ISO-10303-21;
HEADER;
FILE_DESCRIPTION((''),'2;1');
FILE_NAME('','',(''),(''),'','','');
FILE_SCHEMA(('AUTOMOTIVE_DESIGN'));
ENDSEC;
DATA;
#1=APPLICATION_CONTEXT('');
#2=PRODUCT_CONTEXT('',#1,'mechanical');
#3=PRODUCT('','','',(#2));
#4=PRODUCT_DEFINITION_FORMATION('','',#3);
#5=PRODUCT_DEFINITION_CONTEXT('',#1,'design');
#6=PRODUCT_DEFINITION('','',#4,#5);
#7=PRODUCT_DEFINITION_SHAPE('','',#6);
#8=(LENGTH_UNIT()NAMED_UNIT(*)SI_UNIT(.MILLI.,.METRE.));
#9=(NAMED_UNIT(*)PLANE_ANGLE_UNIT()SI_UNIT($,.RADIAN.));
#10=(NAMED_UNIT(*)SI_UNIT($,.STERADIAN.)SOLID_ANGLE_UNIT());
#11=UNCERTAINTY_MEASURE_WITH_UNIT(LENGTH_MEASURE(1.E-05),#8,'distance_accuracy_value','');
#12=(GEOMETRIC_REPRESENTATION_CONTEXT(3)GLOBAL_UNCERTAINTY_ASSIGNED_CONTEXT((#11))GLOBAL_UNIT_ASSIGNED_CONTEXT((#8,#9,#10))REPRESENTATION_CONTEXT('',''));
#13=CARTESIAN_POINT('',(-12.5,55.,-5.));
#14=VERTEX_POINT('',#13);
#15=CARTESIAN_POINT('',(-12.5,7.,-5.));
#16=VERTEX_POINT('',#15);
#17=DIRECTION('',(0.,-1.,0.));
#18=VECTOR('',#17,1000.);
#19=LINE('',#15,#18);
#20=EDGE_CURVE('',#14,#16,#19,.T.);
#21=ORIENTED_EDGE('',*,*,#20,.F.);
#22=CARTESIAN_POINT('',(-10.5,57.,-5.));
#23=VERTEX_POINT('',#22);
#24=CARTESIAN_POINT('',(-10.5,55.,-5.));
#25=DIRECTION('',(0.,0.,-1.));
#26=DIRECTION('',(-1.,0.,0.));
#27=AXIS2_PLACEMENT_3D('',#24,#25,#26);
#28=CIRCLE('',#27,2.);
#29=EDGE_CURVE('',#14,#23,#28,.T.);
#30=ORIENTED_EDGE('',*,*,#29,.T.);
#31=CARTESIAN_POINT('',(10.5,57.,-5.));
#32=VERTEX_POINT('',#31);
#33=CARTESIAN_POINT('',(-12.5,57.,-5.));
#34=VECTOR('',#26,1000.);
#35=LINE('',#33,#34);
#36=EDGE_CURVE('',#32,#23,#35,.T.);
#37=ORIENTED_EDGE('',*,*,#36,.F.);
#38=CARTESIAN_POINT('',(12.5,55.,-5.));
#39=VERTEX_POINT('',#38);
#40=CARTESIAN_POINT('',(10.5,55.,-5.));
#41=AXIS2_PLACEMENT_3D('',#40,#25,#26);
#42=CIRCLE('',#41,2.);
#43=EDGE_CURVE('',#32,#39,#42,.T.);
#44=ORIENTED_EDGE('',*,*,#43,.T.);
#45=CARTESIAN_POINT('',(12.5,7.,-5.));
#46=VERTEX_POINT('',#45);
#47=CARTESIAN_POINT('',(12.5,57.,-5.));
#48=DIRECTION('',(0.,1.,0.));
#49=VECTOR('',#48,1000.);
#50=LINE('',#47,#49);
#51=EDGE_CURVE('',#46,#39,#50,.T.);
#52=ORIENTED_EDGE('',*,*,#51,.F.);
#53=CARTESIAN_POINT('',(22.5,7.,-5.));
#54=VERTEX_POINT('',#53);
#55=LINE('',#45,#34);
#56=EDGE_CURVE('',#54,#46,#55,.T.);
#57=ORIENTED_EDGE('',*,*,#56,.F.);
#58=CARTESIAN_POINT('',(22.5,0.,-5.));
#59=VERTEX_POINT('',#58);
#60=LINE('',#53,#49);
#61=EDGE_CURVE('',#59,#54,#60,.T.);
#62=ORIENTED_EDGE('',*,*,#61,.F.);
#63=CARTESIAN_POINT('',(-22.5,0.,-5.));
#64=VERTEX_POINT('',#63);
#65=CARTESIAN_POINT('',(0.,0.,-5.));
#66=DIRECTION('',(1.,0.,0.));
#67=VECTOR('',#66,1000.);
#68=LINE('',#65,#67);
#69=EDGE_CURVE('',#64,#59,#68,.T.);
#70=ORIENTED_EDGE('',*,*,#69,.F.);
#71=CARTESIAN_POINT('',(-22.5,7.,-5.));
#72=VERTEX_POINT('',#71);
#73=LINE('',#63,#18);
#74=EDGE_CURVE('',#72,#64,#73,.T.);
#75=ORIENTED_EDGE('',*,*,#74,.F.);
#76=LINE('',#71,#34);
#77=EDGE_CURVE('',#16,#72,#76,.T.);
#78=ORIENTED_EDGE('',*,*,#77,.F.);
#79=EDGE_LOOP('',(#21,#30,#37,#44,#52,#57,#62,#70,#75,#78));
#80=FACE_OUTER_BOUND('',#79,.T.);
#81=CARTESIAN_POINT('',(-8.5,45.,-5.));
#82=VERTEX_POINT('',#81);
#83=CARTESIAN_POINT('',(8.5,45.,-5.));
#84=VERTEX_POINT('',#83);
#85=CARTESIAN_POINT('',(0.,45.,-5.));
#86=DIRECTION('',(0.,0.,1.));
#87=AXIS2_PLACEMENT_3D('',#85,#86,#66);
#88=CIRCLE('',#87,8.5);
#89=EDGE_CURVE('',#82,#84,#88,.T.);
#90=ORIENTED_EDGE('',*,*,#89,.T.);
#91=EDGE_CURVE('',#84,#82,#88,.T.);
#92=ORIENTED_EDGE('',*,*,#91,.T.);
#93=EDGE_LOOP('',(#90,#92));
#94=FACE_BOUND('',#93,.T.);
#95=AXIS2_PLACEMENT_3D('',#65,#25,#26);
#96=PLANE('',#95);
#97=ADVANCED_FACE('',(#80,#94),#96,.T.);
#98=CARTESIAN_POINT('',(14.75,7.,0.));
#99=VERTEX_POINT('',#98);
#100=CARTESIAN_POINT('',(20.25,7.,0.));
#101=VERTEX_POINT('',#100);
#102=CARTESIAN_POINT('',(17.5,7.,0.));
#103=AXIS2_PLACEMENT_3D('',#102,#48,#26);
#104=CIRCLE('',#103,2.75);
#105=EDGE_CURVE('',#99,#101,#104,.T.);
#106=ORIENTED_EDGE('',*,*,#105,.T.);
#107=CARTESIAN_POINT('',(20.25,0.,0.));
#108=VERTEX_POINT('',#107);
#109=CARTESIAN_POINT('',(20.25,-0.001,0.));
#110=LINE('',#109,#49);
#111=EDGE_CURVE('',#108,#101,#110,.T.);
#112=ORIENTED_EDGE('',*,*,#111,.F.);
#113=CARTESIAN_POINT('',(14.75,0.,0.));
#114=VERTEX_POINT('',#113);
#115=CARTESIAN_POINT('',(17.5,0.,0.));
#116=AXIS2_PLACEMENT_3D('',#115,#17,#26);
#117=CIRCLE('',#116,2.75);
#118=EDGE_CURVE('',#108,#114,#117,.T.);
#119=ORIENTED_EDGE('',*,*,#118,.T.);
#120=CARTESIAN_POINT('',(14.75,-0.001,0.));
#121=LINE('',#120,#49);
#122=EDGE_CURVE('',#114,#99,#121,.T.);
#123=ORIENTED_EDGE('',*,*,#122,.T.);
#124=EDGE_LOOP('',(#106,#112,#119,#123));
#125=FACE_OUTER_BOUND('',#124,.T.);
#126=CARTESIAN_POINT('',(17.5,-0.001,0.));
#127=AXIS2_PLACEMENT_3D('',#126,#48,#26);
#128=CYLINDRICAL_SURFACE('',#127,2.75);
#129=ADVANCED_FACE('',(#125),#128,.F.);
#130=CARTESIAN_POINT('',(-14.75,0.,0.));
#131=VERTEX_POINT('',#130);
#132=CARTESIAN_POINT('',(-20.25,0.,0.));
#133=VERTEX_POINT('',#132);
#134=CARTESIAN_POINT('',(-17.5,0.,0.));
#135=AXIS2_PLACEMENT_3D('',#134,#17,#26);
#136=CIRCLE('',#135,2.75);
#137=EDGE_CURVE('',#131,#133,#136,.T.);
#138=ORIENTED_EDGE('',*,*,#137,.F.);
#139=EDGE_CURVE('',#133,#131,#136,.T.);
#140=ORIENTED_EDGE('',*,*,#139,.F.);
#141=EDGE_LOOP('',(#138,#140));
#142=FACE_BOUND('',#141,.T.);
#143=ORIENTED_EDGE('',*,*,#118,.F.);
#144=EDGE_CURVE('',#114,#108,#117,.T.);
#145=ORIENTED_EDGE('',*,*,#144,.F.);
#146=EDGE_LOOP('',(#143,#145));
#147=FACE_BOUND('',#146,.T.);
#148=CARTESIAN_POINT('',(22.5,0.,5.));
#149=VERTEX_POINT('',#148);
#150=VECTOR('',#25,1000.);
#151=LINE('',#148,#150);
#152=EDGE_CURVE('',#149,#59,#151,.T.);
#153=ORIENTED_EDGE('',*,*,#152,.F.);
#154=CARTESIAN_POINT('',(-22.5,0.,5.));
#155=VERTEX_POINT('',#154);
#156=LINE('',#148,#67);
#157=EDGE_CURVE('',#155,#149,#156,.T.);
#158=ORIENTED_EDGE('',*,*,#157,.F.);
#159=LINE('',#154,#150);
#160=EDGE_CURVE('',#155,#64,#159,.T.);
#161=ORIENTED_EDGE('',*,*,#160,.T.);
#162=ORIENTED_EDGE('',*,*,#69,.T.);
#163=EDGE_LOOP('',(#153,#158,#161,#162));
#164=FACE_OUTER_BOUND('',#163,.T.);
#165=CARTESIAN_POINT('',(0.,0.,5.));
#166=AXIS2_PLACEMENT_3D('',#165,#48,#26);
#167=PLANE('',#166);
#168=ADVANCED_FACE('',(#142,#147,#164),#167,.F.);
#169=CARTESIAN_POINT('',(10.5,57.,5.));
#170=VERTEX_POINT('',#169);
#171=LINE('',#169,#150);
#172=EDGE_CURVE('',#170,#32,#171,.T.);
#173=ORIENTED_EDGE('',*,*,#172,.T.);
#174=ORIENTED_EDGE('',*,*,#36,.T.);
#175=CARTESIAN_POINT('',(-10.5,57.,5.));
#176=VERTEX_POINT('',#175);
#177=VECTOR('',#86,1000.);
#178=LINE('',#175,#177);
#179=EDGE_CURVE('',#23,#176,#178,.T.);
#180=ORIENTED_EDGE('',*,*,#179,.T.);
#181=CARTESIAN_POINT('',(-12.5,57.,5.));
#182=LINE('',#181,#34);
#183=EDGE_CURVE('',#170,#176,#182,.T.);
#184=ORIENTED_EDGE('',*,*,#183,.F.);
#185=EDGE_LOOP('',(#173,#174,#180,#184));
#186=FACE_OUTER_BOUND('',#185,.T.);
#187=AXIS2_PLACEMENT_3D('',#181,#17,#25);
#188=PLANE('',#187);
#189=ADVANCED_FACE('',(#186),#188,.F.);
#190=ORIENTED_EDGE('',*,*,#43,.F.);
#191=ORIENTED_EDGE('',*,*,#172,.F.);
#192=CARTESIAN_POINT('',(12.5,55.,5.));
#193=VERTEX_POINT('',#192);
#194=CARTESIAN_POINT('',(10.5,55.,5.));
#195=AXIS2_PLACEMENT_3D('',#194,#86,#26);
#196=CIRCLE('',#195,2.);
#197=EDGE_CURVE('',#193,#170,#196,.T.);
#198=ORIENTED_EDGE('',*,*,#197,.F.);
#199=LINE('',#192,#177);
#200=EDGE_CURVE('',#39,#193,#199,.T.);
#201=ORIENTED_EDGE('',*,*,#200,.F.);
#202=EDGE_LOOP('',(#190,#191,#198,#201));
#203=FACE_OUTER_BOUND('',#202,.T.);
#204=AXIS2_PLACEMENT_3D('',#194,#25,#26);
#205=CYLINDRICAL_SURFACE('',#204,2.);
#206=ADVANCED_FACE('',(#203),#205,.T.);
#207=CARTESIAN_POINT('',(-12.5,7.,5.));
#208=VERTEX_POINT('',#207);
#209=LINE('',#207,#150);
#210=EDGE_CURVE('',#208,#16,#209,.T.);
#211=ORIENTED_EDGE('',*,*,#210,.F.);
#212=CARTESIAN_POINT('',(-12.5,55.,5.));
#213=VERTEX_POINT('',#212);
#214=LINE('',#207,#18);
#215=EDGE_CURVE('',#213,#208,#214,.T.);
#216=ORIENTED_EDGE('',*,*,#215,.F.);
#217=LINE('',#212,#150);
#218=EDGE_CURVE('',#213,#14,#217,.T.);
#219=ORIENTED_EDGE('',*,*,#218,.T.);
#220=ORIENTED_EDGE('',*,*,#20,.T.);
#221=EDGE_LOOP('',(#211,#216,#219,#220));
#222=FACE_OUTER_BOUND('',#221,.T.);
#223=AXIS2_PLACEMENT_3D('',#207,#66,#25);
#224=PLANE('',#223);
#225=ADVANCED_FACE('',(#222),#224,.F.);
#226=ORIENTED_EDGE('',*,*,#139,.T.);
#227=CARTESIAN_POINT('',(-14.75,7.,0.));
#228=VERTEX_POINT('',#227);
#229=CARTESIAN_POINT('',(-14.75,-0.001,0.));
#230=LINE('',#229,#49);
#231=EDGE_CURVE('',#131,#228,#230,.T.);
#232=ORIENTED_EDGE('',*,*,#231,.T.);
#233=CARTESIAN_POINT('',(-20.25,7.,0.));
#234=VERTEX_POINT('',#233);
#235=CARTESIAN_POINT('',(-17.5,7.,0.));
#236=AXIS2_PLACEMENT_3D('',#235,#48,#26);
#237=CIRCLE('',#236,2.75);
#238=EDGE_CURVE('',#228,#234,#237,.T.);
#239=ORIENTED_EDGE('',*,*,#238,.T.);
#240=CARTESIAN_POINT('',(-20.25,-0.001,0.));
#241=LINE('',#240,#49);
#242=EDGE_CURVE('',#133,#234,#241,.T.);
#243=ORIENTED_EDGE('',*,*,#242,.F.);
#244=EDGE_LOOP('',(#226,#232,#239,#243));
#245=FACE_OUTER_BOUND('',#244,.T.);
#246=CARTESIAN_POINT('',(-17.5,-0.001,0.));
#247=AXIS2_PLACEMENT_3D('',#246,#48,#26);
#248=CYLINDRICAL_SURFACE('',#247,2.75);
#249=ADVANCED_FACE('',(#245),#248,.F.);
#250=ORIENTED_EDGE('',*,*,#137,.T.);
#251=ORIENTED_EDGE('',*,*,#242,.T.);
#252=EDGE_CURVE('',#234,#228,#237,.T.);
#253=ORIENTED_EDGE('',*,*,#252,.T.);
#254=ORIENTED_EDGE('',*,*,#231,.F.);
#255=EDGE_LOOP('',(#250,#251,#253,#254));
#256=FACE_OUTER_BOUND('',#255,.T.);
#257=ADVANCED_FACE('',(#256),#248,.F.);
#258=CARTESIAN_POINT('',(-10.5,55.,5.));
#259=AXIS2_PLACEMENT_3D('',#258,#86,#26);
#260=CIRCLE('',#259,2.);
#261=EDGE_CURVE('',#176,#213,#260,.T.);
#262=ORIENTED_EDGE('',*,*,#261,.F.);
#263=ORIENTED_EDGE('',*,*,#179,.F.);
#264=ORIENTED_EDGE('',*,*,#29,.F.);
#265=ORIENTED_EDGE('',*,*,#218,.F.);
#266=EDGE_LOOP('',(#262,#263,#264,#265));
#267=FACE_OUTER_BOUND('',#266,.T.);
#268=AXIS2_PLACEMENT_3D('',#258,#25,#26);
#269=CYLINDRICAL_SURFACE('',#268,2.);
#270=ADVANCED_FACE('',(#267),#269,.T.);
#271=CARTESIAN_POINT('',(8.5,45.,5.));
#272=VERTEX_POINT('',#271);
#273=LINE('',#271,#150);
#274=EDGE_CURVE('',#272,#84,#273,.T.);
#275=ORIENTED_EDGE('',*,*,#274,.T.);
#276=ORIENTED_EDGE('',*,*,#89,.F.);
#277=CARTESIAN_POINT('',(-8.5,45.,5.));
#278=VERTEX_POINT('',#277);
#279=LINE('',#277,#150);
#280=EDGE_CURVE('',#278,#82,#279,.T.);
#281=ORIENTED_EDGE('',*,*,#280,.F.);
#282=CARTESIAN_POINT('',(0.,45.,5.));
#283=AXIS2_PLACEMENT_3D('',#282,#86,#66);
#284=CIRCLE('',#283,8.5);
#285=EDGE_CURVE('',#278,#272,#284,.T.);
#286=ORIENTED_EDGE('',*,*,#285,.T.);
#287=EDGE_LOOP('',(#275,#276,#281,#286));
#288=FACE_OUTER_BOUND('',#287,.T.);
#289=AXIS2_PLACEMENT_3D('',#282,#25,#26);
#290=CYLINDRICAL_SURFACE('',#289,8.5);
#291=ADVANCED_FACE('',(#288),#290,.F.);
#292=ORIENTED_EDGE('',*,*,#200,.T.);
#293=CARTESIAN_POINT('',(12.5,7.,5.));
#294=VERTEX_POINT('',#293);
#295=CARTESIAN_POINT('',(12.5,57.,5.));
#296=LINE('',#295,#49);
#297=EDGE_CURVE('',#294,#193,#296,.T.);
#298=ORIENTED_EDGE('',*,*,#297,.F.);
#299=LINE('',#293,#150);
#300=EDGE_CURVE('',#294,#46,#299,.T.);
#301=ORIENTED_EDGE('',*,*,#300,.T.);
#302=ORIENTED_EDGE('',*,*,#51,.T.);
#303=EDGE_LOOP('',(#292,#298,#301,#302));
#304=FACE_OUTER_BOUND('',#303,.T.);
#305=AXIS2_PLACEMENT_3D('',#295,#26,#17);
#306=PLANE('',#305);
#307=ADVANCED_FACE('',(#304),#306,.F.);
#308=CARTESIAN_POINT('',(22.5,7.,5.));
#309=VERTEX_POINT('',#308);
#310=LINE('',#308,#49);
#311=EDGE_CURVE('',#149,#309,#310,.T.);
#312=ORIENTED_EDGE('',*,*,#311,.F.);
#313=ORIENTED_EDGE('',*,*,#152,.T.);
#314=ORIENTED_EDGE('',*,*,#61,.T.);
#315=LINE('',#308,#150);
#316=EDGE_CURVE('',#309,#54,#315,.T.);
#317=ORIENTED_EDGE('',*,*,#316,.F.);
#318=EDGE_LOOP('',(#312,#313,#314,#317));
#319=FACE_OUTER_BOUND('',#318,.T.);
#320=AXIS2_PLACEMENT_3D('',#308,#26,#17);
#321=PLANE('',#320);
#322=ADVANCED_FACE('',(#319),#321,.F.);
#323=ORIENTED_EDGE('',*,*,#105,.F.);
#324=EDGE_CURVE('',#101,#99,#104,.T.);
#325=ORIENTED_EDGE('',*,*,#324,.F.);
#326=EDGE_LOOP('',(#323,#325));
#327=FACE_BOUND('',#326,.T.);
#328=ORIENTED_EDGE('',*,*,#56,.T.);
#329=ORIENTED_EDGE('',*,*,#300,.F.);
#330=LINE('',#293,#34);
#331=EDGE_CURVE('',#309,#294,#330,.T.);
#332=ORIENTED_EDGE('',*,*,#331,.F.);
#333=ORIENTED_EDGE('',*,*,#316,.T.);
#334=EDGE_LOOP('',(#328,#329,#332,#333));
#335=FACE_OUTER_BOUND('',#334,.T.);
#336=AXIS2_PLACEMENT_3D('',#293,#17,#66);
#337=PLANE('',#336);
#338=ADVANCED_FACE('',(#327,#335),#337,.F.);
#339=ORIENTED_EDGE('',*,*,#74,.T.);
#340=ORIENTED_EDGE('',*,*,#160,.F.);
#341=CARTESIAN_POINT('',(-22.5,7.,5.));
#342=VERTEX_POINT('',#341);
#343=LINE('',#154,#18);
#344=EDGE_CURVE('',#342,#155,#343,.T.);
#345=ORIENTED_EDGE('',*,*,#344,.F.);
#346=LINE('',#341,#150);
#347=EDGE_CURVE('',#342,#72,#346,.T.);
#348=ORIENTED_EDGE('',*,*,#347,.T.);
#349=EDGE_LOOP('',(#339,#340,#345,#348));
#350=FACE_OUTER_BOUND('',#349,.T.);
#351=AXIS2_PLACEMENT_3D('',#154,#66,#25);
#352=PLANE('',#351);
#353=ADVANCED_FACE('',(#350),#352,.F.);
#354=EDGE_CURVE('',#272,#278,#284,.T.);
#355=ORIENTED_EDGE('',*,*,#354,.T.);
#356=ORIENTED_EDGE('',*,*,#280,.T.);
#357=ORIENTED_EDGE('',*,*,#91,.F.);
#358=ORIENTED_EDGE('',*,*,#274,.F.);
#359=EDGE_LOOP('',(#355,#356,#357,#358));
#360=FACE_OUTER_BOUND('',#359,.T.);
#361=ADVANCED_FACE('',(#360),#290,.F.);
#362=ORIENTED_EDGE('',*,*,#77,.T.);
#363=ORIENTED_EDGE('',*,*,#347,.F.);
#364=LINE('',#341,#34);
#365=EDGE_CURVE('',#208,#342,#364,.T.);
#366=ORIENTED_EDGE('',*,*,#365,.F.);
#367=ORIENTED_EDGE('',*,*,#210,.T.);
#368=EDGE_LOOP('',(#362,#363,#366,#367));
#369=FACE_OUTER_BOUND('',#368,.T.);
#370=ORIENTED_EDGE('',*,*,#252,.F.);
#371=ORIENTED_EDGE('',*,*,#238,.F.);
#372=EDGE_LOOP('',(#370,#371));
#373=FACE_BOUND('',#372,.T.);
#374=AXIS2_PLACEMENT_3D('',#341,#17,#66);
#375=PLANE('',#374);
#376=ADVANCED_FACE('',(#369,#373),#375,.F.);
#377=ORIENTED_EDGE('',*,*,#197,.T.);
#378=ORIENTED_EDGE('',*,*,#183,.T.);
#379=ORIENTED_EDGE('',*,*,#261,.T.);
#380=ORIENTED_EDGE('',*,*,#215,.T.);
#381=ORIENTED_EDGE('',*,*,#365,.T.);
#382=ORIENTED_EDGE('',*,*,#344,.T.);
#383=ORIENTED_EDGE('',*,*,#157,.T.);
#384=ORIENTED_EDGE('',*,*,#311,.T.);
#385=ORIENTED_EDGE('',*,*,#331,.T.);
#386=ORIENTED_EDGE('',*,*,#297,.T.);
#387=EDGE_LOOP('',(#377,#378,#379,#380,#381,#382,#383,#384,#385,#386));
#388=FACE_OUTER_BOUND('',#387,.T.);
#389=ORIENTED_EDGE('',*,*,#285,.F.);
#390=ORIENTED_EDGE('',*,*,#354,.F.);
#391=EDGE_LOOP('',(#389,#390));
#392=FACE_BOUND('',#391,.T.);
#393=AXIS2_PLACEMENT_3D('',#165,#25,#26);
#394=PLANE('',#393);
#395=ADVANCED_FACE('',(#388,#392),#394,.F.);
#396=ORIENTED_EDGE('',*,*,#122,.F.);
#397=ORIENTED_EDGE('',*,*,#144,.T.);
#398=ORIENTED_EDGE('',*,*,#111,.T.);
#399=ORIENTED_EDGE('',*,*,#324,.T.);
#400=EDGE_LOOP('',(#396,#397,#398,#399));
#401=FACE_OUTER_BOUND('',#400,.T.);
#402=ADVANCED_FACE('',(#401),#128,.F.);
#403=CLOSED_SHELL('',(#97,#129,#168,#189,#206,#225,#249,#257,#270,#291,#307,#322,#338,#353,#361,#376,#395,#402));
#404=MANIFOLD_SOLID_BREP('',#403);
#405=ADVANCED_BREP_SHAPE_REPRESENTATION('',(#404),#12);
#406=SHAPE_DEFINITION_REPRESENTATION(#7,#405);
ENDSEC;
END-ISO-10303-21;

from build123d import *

# Parameters (mm, degrees)
SKETCH_1_R          = 8.5
EXTRUDE_1_DEPTH     = 5
FILLET_1_R          = 2
CUT_EXTRUDE_1_REACH = 57.057
SKETCH_2_R          = 2.75


with BuildPart() as part:
    # 草图1 → 凸台-拉伸1 (new, symmetric)
    with BuildSketch(Plane.XY):
        Polygon((0, 0), (-22.5, 0), (-22.5, 7), (-12.5, 7), (-12.5, 57), (12.5, 57), (12.5, 7), (22.5, 7), (22.5, 0), align=None)
        with Locations((0, 45)):
            Circle(SKETCH_1_R, mode=Mode.SUBTRACT)
    extrude(amount=EXTRUDE_1_DEPTH, both=True)

    # 圆角1
    fillet_1_edges = [part.edges().sort_by_distance(p)[0] for p in [
        (-12.5, 57, 0),
        (12.5, 57, 0),
    ]]
    fillet(fillet_1_edges, radius=FILLET_1_R)

    # 草图2 → 切除-拉伸1 (cut, up to next)
    with BuildSketch(Plane(origin=(0, 7, 0), x_dir=(1, 0, 0), z_dir=(0, 1, 0)), mode=Mode.PRIVATE) as cut_extrude_1_sk1:
        with Locations(Location((-17.5, 0, 0), (0, 0, 180))):
            Circle(SKETCH_2_R)
    cut_extrude_1_tool1 = extrude(cut_extrude_1_sk1.sketch, amount=-CUT_EXTRUDE_1_REACH, mode=Mode.PRIVATE) & part.part
    # 草图2 → 切除-拉伸1 (cut, up to next)
    with BuildSketch(Plane(origin=(0, 7, 0), x_dir=(1, 0, 0), z_dir=(0, 1, 0)), mode=Mode.PRIVATE) as cut_extrude_1_sk2:
        with Locations(Location((17.5, 0, 0), (0, 0, 180))):
            Circle(SKETCH_2_R)
    cut_extrude_1_tool2 = extrude(cut_extrude_1_sk2.sketch, amount=-CUT_EXTRUDE_1_REACH, mode=Mode.PRIVATE) & part.part
    add(cut_extrude_1_tool1.solids().sort_by_distance((-17.5, 7, 0))[0], mode=Mode.SUBTRACT)
    add(cut_extrude_1_tool2.solids().sort_by_distance((17.5, 7, 0))[0], mode=Mode.SUBTRACT)


solid = part.part
